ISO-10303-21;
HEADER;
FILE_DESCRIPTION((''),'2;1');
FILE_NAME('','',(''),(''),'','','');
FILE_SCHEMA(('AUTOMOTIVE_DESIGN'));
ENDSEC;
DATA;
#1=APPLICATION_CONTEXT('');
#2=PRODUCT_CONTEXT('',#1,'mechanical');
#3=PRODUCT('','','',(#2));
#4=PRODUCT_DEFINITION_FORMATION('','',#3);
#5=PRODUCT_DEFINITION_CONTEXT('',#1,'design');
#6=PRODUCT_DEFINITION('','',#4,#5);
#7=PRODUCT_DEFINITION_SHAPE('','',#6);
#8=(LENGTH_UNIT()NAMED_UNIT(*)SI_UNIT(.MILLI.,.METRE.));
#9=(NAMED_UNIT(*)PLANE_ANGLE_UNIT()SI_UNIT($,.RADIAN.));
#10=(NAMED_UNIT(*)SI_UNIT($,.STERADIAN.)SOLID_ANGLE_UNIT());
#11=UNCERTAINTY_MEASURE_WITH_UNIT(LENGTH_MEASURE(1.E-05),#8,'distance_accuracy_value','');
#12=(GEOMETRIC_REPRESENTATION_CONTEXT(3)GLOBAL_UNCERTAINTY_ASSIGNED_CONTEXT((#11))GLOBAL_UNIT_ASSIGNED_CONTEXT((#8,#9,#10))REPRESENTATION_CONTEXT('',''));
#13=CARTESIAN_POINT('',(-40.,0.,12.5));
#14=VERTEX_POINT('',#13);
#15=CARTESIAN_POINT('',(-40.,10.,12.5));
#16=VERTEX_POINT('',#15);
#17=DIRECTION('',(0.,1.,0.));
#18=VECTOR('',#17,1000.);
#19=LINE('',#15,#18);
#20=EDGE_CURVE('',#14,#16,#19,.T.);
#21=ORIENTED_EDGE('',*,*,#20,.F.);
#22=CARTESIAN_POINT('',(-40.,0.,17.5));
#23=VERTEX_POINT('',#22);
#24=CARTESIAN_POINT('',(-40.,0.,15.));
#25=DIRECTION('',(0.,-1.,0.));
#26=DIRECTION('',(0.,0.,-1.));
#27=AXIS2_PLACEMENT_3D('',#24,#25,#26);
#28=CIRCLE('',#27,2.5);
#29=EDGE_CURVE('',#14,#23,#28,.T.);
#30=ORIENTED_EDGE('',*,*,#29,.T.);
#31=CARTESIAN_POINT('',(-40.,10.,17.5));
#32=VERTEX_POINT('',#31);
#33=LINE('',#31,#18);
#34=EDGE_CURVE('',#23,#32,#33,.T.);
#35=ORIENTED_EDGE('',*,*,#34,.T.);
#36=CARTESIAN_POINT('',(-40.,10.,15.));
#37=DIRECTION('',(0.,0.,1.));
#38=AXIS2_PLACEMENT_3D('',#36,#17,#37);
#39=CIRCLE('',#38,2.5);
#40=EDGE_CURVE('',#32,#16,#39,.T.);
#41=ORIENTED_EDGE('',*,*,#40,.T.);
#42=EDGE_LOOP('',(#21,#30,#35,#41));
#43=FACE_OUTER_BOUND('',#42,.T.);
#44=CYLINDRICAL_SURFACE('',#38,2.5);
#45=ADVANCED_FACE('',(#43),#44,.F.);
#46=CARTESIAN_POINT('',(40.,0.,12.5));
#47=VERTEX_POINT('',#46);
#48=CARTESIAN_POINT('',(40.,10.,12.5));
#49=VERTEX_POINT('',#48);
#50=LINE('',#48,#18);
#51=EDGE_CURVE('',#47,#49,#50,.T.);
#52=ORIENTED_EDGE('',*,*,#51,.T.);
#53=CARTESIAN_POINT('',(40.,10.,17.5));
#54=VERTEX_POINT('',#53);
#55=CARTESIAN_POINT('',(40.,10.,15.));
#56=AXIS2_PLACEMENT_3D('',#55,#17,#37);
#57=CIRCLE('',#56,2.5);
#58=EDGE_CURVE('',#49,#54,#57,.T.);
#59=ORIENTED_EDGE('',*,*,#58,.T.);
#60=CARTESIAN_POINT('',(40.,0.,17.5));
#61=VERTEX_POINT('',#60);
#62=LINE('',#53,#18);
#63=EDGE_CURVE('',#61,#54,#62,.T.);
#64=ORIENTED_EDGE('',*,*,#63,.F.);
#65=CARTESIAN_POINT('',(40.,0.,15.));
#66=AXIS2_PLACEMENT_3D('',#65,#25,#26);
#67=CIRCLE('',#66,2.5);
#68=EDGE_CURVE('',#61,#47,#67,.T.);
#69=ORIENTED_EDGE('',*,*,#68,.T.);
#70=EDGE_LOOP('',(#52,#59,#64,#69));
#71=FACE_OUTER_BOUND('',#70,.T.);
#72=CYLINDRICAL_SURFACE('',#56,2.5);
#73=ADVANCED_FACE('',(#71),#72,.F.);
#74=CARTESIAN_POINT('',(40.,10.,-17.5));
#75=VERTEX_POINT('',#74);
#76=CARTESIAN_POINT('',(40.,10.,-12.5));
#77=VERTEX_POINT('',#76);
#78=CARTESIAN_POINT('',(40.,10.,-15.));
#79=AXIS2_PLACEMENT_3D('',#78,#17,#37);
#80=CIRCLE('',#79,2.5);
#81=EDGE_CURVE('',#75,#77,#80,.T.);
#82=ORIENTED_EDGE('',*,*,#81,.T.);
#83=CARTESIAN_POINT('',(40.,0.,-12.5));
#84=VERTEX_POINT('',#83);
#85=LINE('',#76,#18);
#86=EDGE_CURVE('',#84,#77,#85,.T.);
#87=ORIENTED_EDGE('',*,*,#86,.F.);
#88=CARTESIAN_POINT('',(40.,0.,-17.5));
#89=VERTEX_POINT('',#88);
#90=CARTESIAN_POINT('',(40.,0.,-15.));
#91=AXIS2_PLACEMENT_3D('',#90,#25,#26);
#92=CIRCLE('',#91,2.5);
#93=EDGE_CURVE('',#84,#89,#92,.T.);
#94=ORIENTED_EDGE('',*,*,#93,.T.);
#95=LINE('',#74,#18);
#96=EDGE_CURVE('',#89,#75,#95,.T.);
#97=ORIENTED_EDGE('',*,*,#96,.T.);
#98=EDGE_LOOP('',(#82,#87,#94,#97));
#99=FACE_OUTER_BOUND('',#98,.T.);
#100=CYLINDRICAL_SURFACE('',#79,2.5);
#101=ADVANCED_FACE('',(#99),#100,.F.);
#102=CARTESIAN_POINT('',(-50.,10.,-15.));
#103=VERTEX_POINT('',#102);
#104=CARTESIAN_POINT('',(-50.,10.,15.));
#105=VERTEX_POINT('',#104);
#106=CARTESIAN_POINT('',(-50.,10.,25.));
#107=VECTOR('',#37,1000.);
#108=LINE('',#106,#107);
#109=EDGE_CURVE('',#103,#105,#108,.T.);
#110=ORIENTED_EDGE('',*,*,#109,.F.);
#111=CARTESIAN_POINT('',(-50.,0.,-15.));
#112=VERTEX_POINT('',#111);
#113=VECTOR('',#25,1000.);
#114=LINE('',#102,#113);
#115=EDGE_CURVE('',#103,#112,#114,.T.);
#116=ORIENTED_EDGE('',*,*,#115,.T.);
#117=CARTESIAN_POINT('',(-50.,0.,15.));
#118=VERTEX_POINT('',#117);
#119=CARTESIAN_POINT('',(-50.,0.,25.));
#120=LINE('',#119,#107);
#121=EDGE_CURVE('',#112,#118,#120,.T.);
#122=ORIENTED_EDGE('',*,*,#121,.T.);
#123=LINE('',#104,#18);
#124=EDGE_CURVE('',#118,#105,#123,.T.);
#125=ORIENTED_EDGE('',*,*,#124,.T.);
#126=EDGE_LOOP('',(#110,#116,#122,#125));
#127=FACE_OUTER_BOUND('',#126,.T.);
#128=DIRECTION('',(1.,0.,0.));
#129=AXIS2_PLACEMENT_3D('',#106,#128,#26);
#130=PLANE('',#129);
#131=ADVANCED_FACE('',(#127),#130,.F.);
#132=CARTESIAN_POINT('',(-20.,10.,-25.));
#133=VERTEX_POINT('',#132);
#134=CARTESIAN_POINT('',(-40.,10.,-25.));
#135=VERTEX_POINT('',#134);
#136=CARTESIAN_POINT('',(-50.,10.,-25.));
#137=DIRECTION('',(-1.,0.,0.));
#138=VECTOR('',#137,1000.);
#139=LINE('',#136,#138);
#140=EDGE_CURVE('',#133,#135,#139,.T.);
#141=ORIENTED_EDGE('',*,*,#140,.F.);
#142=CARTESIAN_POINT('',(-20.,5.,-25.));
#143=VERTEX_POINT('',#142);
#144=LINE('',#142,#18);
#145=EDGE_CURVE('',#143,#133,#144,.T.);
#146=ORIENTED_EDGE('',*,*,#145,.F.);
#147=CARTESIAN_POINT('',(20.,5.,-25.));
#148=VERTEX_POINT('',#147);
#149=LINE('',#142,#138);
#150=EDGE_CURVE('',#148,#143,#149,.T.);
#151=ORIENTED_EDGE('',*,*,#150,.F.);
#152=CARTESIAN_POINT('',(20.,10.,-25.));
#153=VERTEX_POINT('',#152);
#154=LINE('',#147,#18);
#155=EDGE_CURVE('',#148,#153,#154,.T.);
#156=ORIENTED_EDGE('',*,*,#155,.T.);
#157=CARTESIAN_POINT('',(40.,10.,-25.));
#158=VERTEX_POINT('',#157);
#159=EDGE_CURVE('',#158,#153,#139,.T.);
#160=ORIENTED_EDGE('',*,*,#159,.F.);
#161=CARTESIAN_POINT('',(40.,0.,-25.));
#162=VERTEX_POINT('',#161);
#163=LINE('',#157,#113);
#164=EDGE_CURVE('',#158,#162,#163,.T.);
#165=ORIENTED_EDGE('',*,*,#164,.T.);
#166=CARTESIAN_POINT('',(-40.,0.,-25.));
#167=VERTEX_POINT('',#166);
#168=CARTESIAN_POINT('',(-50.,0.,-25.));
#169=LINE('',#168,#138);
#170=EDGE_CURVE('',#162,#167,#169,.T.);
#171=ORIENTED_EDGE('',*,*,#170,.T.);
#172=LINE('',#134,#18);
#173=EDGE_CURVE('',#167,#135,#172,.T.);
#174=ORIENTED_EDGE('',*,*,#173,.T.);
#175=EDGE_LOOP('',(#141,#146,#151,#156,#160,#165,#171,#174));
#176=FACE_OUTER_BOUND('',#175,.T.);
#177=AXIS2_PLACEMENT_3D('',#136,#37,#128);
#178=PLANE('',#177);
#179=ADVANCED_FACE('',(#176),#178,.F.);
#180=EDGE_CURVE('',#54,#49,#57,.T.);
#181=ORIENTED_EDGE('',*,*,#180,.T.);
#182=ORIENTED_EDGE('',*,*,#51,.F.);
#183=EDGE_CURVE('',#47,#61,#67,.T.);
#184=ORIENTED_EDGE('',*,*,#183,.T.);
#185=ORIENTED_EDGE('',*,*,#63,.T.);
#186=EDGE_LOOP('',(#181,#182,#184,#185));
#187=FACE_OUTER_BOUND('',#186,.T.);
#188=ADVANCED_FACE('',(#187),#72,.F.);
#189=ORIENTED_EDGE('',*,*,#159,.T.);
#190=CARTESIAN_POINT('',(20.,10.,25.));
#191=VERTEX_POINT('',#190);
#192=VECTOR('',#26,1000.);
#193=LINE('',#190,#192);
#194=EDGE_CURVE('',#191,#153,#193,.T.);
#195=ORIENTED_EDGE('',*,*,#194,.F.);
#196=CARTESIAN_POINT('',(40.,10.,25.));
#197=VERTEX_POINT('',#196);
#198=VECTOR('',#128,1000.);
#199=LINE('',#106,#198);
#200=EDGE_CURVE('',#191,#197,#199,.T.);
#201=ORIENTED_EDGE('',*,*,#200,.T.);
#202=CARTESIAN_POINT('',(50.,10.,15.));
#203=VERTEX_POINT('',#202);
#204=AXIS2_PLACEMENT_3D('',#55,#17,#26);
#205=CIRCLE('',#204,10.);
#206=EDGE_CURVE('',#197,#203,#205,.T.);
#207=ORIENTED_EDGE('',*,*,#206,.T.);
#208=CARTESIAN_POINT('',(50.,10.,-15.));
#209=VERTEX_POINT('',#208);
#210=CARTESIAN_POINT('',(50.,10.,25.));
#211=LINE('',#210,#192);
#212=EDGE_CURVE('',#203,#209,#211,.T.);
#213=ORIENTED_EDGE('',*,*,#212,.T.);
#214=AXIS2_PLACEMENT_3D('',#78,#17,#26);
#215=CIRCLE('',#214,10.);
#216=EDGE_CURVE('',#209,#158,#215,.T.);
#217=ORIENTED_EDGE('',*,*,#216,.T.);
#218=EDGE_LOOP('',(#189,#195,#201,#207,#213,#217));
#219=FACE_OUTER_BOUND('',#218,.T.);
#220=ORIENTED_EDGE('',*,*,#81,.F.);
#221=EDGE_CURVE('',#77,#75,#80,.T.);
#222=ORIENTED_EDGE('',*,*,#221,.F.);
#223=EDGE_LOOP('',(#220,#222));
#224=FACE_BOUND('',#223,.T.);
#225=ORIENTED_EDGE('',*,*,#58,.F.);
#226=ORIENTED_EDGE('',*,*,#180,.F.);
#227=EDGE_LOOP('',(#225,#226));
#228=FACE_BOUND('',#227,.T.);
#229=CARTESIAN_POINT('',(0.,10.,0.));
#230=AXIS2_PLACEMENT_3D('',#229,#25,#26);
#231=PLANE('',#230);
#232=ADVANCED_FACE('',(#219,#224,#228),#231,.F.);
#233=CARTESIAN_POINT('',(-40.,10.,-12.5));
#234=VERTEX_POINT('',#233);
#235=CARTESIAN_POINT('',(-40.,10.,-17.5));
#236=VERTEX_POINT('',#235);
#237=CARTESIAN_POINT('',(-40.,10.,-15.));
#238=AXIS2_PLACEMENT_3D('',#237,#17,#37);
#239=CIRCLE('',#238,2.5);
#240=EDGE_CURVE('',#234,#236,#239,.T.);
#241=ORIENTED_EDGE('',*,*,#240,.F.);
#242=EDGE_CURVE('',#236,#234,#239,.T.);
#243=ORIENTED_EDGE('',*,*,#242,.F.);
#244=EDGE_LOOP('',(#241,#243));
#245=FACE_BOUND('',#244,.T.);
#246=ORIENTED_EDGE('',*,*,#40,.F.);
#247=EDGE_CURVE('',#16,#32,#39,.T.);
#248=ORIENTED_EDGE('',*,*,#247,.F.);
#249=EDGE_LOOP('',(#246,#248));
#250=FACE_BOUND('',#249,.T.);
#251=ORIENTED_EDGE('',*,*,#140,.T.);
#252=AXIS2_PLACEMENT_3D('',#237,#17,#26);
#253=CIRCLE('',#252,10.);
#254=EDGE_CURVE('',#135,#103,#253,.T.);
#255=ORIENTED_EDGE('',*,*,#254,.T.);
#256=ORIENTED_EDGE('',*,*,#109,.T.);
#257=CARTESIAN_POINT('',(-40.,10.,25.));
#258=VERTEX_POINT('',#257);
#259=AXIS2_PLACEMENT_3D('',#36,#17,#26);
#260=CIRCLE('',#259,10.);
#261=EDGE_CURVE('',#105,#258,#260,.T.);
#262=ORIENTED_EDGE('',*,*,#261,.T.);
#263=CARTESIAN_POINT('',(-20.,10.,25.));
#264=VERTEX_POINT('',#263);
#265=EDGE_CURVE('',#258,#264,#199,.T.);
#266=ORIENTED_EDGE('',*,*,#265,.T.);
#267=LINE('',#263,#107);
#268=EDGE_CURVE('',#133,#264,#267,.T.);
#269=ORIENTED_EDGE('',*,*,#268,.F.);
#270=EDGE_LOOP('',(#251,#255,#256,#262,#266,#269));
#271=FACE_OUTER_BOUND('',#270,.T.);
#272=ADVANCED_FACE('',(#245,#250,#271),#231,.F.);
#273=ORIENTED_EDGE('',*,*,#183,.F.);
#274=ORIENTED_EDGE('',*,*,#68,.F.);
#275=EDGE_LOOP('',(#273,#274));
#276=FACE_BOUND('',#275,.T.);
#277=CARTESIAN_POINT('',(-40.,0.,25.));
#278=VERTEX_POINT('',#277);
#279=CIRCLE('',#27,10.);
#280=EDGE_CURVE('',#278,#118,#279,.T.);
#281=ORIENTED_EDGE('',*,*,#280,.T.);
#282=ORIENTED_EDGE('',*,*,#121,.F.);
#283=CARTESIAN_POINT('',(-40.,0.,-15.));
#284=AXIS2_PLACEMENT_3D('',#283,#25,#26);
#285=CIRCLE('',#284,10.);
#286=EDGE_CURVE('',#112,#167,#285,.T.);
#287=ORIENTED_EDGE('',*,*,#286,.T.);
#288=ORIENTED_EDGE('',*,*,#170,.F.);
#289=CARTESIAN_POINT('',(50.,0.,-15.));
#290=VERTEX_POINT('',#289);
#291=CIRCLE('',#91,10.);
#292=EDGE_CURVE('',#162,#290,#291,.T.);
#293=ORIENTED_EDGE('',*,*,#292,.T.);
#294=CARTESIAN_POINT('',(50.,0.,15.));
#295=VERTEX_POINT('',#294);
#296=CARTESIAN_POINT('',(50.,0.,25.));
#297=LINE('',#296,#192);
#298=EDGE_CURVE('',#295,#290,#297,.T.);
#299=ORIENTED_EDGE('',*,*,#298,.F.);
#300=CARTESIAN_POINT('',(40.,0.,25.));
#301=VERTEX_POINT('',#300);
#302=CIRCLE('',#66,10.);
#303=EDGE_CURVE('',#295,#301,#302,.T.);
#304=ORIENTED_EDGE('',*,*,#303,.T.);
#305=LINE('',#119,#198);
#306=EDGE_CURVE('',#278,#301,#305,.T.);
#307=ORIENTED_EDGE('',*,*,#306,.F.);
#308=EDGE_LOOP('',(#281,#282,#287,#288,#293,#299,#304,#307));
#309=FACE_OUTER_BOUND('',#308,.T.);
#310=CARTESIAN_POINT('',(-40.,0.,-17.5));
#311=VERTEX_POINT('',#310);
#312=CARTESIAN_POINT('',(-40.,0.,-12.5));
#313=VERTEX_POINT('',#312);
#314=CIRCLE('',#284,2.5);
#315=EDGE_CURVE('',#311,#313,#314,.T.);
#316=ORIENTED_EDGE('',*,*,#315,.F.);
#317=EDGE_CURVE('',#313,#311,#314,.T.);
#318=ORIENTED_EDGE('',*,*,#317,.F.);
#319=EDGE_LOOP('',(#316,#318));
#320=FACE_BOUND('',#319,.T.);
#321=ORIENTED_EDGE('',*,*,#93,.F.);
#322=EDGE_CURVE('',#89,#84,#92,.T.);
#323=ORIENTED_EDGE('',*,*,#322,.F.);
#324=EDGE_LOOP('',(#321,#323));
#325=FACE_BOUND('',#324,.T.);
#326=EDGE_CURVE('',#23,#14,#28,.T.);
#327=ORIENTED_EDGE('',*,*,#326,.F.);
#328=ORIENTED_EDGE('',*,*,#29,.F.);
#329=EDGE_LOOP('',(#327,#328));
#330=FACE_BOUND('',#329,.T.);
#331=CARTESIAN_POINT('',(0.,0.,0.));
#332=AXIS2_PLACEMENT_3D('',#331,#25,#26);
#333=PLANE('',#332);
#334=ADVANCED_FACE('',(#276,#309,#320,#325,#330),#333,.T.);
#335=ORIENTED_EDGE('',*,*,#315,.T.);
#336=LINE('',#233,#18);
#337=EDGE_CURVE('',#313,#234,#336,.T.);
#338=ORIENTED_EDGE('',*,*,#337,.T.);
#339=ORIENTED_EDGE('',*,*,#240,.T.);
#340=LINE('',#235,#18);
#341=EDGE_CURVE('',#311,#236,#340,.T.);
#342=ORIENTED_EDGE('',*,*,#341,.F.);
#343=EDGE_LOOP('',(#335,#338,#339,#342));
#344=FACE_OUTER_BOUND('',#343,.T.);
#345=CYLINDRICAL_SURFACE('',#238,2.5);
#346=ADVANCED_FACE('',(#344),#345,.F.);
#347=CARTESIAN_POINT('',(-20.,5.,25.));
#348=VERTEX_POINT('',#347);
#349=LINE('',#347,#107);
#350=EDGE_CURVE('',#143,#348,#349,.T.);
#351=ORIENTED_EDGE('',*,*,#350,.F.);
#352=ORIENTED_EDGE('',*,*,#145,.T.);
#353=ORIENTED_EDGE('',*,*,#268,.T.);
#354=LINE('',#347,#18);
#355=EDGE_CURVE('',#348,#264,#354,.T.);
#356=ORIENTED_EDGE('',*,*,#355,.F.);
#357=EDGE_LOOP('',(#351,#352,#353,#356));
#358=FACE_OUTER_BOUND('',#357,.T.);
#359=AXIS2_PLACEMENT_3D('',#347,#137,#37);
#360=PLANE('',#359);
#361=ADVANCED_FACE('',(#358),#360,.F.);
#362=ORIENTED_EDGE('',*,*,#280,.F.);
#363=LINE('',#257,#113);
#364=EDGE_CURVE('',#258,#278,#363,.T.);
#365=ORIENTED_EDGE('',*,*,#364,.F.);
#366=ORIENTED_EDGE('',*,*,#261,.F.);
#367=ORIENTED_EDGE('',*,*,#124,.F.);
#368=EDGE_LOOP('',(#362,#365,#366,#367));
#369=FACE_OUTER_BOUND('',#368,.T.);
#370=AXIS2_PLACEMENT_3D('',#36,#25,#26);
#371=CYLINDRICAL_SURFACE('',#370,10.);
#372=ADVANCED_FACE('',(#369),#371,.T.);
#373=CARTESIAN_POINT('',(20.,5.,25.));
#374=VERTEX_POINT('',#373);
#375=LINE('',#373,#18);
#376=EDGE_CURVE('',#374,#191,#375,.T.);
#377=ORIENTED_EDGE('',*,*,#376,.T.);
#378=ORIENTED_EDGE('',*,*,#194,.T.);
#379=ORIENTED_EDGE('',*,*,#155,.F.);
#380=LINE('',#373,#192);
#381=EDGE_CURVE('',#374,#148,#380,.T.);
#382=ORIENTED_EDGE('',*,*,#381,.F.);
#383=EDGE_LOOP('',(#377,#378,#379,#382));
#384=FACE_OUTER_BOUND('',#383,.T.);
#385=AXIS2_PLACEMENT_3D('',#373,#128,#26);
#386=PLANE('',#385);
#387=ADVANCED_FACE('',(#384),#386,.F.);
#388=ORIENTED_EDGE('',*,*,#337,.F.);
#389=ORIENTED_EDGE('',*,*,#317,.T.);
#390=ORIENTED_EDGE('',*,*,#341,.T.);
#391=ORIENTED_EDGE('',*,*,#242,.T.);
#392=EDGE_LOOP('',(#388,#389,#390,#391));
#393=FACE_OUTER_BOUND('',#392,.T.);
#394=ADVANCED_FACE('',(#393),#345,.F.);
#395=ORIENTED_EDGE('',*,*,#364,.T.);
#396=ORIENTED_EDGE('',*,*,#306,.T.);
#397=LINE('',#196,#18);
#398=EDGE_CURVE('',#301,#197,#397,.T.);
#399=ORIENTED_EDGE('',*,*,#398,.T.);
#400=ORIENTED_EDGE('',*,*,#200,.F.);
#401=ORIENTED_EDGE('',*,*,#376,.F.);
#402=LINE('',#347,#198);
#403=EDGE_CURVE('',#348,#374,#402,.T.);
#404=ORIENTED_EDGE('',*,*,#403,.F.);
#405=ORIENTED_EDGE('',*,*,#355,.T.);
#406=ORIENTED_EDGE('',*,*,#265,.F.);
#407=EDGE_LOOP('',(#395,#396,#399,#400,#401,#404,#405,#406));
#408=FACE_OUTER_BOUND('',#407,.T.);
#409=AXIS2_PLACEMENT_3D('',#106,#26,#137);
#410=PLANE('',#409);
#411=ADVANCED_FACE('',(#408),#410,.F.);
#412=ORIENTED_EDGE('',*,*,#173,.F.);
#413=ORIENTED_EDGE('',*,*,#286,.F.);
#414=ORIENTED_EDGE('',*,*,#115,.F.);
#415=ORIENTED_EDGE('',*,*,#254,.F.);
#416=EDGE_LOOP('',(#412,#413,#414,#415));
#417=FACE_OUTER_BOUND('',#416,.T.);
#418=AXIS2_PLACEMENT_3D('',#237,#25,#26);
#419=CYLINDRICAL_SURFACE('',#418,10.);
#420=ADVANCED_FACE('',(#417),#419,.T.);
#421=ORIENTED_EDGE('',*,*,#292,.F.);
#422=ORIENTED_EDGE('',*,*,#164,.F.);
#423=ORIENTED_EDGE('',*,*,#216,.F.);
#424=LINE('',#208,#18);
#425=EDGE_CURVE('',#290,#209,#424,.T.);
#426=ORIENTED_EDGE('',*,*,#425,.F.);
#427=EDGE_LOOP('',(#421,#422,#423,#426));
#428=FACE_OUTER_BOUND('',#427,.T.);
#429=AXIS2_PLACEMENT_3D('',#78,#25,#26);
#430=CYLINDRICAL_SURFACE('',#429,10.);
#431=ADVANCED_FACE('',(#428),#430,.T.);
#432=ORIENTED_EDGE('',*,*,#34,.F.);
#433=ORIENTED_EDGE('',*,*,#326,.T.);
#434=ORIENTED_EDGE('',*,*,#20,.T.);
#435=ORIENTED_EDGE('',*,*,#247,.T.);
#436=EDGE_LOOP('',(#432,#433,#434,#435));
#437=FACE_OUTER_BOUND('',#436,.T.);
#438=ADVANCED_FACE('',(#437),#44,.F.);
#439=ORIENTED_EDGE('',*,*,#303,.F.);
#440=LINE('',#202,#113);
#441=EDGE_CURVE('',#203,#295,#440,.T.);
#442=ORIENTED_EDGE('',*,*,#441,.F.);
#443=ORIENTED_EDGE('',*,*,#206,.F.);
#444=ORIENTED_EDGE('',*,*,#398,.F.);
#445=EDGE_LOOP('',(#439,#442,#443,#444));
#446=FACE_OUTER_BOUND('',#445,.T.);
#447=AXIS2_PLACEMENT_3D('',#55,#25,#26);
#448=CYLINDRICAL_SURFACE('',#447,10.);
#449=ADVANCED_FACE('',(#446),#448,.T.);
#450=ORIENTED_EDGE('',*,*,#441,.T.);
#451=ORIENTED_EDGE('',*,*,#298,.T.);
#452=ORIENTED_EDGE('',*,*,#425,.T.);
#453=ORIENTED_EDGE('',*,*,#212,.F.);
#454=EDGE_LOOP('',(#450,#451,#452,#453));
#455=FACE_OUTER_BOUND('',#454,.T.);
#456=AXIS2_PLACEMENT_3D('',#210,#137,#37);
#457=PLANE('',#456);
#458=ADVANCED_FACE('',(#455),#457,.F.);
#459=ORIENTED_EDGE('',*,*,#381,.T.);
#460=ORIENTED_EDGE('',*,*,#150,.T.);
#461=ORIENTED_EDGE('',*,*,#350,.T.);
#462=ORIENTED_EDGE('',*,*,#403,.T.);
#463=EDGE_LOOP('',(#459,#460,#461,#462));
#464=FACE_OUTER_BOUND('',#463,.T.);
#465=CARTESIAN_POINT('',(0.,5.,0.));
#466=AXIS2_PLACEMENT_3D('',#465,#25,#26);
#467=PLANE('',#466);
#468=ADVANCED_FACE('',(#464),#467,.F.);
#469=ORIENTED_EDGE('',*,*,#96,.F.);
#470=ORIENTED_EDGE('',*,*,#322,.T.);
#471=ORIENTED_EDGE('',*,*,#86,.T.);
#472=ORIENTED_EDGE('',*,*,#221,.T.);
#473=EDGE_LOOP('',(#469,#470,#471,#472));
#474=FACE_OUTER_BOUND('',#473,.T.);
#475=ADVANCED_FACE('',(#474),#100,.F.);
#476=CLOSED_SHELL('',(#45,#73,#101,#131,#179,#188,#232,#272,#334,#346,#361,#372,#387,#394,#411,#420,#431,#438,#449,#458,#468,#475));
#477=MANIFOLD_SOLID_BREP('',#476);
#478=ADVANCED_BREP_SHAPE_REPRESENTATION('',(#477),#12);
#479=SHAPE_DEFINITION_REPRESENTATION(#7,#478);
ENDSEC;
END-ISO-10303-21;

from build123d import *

# Parameters (mm, degrees)
SKETCH1_W             = 100
SKETCH1_H             = 50
BOSS_EXTRUDE1_DEPTH   = 10
FILLET1_R             = 10
M6_TAPPED_HOLE1_D     = 5
M6_TAPPED_HOLE1_DEPTH = 13.497848452
M6_TAPPED_HOLE1_TIP   = 1.502151548
SKETCH2_W             = 40
SKETCH2_H             = 50
CUT_EXTRUDE1_DEPTH    = 5


with BuildPart() as part:
    # Sketch1 → Boss-Extrude1 (new body)
    with BuildSketch(Plane(origin=(0, 0, 0), x_dir=(1, 0, 0), z_dir=(0, 1, 0))):
        Rectangle(SKETCH1_W, SKETCH1_H)
    extrude(amount=BOSS_EXTRUDE1_DEPTH)

    # Fillet1
    fillet1_edges = [part.edges().sort_by_distance(p)[0] for p in [
        (50, 5, 25),
        (-50, 5, 25),
        (-50, 5, -25),
        (50, 5, -25),
    ]]
    fillet(fillet1_edges, radius=FILLET1_R)

    # M6 Tapped Hole1
    with Locations(Plane(origin=(-40, 10, 15), x_dir=(0, 0, 1), z_dir=(0, 1, 0))):
        with Locations((0, 0), (-30, 0), (-30, 80), (0, 80)):
            Hole(M6_TAPPED_HOLE1_D / 2, depth=M6_TAPPED_HOLE1_DEPTH)
            with Locations((0, 0, -(M6_TAPPED_HOLE1_DEPTH + M6_TAPPED_HOLE1_TIP / 2))):  # 118° drill point
                Cone(0, M6_TAPPED_HOLE1_D / 2, M6_TAPPED_HOLE1_TIP, mode=Mode.SUBTRACT)

    # Sketch2 → Cut-Extrude1 (cut)
    with BuildSketch(Plane(origin=(0, 10, 0), x_dir=(1, 0, 0), z_dir=(0, 1, 0))):
        Rectangle(SKETCH2_W, SKETCH2_H)
    extrude(amount=-CUT_EXTRUDE1_DEPTH, mode=Mode.SUBTRACT)


solid = part.part
